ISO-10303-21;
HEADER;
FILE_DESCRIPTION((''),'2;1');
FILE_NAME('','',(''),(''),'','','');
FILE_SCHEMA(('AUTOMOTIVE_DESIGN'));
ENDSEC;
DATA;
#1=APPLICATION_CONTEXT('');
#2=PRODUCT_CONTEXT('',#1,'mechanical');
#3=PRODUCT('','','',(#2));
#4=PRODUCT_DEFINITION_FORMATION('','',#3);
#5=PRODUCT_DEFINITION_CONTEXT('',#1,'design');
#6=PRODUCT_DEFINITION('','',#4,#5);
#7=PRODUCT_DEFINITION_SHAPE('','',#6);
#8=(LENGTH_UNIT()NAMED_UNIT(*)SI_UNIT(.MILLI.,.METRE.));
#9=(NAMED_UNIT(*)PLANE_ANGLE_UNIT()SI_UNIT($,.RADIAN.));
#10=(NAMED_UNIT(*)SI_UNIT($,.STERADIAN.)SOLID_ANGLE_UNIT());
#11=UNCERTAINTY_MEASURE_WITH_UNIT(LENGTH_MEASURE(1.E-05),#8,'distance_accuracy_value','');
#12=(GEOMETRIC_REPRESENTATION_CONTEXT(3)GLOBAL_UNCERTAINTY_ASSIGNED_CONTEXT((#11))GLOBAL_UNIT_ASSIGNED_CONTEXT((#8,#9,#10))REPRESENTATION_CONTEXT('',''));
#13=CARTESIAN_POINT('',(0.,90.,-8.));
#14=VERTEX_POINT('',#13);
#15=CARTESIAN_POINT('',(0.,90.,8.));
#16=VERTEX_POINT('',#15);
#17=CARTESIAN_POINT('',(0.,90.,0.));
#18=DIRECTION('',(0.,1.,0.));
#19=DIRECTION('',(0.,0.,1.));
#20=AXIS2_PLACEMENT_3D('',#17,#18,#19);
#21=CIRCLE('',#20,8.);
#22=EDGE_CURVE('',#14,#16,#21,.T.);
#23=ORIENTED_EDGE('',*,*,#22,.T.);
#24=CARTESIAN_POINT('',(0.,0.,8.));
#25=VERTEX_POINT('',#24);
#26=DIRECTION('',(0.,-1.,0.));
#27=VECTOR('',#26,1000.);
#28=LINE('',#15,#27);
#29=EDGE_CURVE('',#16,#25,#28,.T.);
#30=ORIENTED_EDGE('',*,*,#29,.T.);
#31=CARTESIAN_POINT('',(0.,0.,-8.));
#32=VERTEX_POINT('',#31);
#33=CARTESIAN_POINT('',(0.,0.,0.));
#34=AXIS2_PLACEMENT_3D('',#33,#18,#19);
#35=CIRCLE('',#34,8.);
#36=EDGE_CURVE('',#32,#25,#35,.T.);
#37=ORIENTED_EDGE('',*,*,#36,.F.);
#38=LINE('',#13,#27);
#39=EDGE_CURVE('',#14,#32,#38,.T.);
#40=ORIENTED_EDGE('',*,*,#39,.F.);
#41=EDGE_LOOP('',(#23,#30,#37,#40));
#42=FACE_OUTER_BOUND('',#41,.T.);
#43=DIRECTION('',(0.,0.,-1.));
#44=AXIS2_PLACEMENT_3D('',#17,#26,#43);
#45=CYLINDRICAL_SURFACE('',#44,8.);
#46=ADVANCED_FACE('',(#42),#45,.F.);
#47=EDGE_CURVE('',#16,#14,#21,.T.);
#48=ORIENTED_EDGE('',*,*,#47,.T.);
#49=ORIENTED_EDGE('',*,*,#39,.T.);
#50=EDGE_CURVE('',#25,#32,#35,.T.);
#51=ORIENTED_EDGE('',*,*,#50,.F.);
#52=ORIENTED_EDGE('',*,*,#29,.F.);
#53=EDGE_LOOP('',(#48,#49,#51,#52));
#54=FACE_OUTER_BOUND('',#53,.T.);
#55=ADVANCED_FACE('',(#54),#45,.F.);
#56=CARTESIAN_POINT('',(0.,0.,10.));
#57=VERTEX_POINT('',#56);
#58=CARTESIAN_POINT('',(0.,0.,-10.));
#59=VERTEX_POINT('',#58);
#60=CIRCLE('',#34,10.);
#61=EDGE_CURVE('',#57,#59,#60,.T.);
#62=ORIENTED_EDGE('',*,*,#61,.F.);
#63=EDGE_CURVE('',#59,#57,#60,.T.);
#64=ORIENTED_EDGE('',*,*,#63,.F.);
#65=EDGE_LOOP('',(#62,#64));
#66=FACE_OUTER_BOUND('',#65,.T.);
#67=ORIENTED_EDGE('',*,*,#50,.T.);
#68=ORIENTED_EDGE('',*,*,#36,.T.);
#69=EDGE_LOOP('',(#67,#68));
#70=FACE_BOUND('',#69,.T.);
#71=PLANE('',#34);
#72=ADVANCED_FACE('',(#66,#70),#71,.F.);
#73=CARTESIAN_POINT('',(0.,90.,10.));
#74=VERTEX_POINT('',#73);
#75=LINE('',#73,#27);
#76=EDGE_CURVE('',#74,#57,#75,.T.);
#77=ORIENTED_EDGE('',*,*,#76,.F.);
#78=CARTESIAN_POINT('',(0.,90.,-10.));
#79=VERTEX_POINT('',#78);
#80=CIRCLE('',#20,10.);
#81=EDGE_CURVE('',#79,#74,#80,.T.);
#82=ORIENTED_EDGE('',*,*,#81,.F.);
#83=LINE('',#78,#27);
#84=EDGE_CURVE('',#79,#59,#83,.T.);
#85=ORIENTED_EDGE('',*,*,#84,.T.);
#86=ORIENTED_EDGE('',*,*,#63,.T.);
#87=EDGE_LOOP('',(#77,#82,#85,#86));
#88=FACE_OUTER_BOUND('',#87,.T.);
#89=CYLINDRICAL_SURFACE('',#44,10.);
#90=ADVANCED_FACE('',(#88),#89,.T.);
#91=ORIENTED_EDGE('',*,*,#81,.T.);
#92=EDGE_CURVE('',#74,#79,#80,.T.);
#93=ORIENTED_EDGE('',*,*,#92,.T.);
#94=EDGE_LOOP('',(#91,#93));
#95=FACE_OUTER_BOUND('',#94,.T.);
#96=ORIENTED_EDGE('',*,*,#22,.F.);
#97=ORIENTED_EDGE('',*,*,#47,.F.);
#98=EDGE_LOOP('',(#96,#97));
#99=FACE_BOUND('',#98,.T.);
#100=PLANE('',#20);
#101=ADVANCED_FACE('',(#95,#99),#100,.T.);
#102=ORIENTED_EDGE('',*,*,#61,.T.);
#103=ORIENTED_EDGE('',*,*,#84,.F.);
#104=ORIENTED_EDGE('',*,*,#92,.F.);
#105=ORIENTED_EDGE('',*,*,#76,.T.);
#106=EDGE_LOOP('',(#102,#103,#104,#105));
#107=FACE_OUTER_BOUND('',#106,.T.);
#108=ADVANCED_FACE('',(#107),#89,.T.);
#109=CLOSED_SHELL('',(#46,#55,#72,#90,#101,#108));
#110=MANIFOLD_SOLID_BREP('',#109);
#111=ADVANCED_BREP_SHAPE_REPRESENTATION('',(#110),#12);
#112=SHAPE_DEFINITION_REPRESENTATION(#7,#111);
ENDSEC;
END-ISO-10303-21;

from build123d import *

# Parameters (mm, degrees)
SKETCH11_R                             = 10
SKETCH11_R_2                           = 8
GB_T_6728_2002_ROUND_TUBE_20_2_1_DEPTH = 90


with BuildPart() as part:
    # Sketch11 → GB/T 6728-2002 round tube 20 × 2(1) (new body)
    with BuildSketch(Plane(origin=(0, 0, 0), x_dir=(-1, 0, 0), z_dir=(0, 1, 0))):
        Circle(SKETCH11_R)
        Circle(SKETCH11_R_2, mode=Mode.SUBTRACT)
    extrude(amount=GB_T_6728_2002_ROUND_TUBE_20_2_1_DEPTH)


solid = part.part
